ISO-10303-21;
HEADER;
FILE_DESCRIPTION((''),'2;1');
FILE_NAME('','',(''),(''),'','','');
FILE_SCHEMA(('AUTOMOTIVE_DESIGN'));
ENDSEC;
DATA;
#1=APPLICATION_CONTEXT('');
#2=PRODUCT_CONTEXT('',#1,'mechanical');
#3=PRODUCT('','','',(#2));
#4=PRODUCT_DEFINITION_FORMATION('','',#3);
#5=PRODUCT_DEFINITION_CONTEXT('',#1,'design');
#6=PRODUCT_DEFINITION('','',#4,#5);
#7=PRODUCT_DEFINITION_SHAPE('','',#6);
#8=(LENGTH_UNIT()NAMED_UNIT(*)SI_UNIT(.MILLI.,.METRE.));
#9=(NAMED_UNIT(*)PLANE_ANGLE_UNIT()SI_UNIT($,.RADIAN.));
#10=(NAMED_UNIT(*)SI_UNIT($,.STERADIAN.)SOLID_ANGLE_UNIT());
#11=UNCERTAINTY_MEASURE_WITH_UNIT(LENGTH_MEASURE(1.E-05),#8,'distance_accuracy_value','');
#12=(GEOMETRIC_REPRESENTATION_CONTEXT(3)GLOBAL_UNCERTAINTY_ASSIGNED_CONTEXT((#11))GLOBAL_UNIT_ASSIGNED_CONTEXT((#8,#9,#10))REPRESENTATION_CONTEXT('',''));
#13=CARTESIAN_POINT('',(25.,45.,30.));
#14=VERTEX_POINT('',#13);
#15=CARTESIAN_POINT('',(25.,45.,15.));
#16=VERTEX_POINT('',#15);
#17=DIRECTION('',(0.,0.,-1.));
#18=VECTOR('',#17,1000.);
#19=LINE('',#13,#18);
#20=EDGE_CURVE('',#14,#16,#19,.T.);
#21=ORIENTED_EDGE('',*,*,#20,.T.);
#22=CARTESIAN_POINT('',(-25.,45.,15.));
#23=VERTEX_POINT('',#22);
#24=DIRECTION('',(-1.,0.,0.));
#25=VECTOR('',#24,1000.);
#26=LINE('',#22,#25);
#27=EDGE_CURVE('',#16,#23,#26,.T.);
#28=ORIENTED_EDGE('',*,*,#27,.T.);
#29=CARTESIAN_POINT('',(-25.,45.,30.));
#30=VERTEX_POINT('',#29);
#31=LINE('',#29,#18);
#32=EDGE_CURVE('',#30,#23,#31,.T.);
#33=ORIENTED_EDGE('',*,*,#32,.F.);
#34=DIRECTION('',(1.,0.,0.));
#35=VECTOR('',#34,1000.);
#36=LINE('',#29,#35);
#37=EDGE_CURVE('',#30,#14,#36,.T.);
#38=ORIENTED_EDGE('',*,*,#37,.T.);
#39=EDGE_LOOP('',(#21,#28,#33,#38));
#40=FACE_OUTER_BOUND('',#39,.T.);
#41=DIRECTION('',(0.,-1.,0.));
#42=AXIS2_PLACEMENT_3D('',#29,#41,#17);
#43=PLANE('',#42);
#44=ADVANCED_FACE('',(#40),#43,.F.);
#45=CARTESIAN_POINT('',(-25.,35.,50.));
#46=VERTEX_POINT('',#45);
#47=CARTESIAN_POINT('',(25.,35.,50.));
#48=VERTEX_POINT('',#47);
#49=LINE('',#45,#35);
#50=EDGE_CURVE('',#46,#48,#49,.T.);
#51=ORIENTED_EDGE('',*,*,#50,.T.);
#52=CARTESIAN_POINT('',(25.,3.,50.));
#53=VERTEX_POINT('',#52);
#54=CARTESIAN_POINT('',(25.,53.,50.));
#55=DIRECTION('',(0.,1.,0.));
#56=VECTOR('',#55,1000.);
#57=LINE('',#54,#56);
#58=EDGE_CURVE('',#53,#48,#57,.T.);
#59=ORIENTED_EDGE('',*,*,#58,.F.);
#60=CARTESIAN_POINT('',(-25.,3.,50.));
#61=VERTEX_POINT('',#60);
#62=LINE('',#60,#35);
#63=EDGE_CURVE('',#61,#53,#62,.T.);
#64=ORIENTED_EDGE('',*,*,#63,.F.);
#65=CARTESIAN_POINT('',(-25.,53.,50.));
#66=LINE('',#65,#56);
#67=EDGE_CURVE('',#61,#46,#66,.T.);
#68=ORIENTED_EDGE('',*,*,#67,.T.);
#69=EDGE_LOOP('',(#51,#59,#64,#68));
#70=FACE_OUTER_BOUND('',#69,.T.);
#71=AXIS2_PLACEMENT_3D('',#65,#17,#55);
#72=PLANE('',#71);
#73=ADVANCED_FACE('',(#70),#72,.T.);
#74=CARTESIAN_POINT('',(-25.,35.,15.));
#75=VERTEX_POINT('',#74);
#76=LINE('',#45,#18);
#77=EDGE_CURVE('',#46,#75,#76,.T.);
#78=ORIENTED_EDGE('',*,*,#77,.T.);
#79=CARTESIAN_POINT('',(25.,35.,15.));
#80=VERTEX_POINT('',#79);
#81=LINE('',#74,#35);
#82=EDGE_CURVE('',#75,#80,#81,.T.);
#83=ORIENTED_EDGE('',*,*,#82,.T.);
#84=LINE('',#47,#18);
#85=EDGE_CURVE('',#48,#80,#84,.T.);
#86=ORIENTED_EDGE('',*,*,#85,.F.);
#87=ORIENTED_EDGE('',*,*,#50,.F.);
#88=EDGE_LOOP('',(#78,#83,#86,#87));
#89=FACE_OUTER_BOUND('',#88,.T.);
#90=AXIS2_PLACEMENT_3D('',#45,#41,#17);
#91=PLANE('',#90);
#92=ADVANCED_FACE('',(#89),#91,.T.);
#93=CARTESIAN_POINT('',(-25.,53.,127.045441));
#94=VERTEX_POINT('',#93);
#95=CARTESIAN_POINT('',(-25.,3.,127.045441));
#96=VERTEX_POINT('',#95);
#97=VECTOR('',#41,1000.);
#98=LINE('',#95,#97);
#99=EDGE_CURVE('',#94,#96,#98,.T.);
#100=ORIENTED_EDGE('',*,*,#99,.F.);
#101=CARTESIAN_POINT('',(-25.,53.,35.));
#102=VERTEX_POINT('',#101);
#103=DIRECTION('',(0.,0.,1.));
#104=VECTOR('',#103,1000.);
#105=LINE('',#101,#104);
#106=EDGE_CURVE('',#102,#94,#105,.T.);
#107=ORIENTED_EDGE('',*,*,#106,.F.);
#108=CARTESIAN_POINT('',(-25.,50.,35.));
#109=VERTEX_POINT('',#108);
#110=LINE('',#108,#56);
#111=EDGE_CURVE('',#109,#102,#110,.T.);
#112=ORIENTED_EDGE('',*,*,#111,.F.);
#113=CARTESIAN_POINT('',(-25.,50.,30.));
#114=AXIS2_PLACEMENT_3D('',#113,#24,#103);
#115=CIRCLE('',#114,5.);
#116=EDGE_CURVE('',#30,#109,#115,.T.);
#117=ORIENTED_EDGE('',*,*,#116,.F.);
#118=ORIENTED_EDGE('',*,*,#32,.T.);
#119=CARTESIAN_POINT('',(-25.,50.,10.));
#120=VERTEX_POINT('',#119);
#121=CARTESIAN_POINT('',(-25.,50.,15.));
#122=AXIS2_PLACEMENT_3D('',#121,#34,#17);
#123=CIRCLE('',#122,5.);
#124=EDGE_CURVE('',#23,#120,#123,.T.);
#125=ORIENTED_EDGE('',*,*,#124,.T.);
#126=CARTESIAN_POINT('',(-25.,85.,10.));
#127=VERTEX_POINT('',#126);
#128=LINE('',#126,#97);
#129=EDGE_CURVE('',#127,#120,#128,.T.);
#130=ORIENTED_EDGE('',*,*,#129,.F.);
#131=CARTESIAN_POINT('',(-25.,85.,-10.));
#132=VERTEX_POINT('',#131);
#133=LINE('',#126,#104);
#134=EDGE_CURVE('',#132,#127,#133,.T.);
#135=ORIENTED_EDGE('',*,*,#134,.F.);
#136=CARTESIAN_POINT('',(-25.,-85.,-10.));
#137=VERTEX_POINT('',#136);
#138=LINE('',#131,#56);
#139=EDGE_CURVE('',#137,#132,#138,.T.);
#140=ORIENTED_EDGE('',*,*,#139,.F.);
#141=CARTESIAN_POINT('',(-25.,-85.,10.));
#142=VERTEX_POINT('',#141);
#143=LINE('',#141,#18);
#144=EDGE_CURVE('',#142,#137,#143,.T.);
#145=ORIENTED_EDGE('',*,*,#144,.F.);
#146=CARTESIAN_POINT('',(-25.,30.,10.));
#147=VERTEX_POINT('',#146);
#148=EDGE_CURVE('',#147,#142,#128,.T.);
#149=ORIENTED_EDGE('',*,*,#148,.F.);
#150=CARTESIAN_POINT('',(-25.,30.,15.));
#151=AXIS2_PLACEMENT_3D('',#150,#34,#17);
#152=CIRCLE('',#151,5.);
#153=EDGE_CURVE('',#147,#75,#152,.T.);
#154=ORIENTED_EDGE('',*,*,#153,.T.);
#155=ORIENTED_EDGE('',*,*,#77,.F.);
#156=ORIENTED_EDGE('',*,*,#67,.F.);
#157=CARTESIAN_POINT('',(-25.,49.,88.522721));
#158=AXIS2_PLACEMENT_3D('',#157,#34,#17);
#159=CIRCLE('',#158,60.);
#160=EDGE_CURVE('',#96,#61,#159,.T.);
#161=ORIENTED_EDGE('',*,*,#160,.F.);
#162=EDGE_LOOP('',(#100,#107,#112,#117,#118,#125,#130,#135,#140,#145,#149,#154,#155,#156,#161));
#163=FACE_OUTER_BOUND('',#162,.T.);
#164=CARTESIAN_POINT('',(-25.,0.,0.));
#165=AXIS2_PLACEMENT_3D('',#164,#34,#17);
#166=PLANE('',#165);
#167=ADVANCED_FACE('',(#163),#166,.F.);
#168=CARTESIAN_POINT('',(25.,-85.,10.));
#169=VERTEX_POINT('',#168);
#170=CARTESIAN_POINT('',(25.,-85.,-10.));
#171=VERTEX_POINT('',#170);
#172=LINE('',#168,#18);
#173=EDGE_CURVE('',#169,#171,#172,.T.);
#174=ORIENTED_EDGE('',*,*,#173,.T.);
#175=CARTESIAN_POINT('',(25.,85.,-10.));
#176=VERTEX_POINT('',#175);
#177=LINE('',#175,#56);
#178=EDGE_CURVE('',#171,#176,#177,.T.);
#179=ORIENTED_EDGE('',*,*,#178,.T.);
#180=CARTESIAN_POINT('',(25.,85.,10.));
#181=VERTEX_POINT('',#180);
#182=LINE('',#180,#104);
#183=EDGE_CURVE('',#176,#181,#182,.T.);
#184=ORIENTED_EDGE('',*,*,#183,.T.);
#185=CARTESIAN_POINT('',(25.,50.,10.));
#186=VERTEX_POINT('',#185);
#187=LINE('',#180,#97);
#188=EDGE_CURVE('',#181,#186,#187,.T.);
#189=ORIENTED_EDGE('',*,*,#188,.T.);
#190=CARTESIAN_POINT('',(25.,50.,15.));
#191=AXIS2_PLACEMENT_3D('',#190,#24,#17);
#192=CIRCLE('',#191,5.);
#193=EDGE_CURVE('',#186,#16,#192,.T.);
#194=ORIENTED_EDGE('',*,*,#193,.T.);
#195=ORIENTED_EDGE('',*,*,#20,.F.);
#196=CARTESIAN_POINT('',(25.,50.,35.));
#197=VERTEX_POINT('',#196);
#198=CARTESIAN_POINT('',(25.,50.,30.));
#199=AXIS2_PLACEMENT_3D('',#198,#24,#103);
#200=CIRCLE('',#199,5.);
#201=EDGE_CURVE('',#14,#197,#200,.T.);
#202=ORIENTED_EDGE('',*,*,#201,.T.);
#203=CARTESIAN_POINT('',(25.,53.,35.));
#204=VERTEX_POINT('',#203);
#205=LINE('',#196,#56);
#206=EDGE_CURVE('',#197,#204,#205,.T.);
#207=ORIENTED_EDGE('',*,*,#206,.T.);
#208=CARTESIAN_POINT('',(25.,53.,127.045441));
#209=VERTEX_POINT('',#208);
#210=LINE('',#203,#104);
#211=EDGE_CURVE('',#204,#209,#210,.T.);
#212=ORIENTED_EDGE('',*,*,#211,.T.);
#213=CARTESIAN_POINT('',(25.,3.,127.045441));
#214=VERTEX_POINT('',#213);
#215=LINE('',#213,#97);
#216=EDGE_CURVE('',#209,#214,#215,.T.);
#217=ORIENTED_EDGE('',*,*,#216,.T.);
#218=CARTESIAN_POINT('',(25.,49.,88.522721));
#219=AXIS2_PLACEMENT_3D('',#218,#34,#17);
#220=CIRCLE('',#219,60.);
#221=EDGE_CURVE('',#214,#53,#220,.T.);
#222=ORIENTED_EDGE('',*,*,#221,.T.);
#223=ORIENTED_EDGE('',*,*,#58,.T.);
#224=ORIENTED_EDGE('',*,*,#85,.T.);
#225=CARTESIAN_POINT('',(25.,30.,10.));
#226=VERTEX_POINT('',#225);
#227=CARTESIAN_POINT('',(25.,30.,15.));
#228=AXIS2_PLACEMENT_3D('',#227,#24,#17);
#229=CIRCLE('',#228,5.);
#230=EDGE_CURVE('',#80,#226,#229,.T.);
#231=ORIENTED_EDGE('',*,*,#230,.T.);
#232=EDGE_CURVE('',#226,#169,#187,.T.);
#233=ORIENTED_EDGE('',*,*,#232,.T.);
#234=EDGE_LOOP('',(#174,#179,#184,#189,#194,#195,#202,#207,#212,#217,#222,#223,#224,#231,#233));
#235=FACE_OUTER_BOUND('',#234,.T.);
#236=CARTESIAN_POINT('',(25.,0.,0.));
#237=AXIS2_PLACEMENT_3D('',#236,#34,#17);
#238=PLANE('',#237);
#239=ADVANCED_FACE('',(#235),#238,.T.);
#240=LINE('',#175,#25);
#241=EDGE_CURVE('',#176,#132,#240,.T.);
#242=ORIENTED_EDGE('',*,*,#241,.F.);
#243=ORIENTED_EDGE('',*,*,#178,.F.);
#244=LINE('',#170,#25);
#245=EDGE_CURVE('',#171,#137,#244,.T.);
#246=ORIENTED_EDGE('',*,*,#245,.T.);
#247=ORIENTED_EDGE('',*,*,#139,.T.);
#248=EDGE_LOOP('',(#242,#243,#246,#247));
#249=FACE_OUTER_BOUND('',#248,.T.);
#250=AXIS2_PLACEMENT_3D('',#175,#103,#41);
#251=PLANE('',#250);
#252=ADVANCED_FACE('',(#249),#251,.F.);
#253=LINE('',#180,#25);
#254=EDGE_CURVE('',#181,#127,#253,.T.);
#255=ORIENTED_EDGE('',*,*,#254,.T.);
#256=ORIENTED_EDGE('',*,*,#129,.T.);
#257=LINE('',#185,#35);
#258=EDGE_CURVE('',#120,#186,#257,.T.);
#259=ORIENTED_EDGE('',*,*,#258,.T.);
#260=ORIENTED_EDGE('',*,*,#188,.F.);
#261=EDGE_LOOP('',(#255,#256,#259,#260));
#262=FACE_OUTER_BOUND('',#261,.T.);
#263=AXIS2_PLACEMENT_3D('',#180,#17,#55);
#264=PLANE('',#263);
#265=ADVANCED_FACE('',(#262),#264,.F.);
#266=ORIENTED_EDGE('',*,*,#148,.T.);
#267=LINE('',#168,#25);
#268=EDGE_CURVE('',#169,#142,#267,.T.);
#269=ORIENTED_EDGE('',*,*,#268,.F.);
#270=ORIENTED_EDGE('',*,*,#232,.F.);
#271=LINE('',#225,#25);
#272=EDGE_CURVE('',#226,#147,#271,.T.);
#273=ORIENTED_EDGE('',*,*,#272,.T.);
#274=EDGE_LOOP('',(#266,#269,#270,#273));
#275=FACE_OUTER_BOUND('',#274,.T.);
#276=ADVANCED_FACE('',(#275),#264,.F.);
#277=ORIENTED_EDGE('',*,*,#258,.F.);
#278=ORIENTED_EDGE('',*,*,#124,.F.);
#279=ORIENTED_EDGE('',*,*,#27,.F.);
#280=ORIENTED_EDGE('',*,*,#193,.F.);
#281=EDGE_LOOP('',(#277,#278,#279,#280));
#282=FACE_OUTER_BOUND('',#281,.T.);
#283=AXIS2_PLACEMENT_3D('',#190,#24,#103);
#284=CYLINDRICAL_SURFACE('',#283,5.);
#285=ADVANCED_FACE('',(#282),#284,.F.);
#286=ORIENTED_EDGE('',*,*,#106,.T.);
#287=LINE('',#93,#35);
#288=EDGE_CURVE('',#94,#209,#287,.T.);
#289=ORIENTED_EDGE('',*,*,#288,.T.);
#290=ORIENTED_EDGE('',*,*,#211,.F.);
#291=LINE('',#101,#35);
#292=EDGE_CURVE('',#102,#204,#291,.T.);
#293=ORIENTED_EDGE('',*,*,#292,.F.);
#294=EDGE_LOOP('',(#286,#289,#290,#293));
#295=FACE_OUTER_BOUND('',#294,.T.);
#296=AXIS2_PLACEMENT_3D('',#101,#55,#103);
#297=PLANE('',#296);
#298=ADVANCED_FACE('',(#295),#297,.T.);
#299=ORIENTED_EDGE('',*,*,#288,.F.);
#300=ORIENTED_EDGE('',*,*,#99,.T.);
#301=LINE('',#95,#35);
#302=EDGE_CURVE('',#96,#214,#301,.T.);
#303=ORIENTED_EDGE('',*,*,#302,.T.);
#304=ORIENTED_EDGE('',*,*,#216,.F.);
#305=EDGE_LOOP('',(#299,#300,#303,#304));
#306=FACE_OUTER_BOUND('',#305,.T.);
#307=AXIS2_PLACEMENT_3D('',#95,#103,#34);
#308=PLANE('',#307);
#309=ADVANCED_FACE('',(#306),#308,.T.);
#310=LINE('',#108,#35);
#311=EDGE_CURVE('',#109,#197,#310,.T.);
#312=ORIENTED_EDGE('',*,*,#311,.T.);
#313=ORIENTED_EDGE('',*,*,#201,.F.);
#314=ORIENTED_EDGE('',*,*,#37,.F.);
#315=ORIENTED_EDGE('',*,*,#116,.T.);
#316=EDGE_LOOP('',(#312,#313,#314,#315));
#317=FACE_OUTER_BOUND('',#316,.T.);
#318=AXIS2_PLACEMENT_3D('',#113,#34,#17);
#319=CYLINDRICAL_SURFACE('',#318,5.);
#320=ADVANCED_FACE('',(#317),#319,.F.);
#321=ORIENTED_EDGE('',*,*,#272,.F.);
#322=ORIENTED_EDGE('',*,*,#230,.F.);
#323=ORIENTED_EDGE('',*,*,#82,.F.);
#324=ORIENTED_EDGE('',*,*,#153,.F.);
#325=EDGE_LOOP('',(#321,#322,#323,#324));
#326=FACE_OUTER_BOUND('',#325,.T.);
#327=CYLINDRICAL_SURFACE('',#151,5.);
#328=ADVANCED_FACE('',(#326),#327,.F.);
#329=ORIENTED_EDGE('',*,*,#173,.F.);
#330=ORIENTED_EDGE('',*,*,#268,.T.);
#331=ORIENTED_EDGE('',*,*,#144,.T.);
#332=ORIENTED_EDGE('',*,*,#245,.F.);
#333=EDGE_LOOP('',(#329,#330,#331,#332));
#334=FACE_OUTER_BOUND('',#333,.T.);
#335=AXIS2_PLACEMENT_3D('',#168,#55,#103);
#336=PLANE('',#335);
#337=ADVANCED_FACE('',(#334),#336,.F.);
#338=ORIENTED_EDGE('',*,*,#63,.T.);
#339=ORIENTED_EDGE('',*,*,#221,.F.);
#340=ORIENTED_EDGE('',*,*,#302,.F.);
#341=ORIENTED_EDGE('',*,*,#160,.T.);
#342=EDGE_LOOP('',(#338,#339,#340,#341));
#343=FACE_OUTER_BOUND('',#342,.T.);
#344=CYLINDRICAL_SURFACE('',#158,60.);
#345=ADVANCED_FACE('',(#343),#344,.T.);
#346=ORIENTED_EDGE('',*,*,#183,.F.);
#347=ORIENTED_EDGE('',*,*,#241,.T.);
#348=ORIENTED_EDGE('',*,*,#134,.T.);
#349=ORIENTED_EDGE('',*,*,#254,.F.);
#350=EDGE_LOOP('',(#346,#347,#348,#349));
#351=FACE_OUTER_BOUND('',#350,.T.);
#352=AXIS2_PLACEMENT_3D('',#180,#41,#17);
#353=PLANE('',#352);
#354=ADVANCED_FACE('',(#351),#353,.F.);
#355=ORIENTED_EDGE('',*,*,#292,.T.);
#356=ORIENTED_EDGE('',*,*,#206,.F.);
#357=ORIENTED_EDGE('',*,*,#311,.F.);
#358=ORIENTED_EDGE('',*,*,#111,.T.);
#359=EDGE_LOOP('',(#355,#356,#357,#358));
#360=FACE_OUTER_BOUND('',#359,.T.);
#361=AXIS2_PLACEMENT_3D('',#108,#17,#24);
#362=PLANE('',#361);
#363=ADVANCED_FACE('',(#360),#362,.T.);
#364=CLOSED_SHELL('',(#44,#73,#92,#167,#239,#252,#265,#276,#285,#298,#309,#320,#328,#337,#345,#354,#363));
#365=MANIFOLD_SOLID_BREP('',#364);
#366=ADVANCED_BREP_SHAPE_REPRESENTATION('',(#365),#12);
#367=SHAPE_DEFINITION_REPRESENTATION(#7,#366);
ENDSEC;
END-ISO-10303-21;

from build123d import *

# Parameters (mm, degrees)
BACK_PLATE_SKETCH_W = 20
BACK_PLATE_SKETCH_H = 170
BACK_PLATE_DEPTH    = 25
NECK_BOSS_DEPTH     = 50
NECK_FILLET_R5_R    = 5
ARM_BLOCK_DEPTH     = 50


with BuildPart() as part:
    # Back Plate Sketch → Back Plate (new, symmetric)
    with BuildSketch(Plane(origin=(0, 0, 0), x_dir=(0, 0, -1), z_dir=(1, 0, 0))):
        Rectangle(BACK_PLATE_SKETCH_W, BACK_PLATE_SKETCH_H)
    extrude(amount=BACK_PLATE_DEPTH, both=True)

    # Neck Boss Sketch → Neck Boss (add, through all)
    with BuildSketch(Plane(origin=(25, 0, 0), x_dir=(0, 0, -1), z_dir=(1, 0, 0))):
        with BuildLine():
            Line((-30, 45), (-10, 45))
            Line((-10, 45), (-10, 35))
            Line((-10, 35), (-50, 35))
            Line((-50, 35), (-50, 53))
            Line((-50, 53), (-35, 53))
            Line((-35, 53), (-35, 50))
            ThreePointArc((-35, 50), (-33.535533906, 46.464466094), (-30, 45))
        make_face()
    extrude(amount=-NECK_BOSS_DEPTH)

    # Neck Fillet R5
    neck_fillet_r5_edges = [part.edges().sort_by_distance(p)[0] for p in [
        (0, 45, 10),
        (0, 35, 10),
    ]]
    fillet(neck_fillet_r5_edges, radius=NECK_FILLET_R5_R)

    # Arm Block Sketch → Arm Block (add, through all)
    with BuildSketch(Plane(origin=(25, 0, 0), x_dir=(0, 0, -1), z_dir=(1, 0, 0))):
        with BuildLine():
            Line((-50, 53), (-50, 3))
            ThreePointArc((-50, 3), (-88.522720569, -11), (-127.045441137, 3))
            Line((-127.045441137, 3), (-127.045441137, 53))
            Line((-127.045441137, 53), (-50, 53))
        make_face()
    extrude(amount=-ARM_BLOCK_DEPTH)


solid = part.part
